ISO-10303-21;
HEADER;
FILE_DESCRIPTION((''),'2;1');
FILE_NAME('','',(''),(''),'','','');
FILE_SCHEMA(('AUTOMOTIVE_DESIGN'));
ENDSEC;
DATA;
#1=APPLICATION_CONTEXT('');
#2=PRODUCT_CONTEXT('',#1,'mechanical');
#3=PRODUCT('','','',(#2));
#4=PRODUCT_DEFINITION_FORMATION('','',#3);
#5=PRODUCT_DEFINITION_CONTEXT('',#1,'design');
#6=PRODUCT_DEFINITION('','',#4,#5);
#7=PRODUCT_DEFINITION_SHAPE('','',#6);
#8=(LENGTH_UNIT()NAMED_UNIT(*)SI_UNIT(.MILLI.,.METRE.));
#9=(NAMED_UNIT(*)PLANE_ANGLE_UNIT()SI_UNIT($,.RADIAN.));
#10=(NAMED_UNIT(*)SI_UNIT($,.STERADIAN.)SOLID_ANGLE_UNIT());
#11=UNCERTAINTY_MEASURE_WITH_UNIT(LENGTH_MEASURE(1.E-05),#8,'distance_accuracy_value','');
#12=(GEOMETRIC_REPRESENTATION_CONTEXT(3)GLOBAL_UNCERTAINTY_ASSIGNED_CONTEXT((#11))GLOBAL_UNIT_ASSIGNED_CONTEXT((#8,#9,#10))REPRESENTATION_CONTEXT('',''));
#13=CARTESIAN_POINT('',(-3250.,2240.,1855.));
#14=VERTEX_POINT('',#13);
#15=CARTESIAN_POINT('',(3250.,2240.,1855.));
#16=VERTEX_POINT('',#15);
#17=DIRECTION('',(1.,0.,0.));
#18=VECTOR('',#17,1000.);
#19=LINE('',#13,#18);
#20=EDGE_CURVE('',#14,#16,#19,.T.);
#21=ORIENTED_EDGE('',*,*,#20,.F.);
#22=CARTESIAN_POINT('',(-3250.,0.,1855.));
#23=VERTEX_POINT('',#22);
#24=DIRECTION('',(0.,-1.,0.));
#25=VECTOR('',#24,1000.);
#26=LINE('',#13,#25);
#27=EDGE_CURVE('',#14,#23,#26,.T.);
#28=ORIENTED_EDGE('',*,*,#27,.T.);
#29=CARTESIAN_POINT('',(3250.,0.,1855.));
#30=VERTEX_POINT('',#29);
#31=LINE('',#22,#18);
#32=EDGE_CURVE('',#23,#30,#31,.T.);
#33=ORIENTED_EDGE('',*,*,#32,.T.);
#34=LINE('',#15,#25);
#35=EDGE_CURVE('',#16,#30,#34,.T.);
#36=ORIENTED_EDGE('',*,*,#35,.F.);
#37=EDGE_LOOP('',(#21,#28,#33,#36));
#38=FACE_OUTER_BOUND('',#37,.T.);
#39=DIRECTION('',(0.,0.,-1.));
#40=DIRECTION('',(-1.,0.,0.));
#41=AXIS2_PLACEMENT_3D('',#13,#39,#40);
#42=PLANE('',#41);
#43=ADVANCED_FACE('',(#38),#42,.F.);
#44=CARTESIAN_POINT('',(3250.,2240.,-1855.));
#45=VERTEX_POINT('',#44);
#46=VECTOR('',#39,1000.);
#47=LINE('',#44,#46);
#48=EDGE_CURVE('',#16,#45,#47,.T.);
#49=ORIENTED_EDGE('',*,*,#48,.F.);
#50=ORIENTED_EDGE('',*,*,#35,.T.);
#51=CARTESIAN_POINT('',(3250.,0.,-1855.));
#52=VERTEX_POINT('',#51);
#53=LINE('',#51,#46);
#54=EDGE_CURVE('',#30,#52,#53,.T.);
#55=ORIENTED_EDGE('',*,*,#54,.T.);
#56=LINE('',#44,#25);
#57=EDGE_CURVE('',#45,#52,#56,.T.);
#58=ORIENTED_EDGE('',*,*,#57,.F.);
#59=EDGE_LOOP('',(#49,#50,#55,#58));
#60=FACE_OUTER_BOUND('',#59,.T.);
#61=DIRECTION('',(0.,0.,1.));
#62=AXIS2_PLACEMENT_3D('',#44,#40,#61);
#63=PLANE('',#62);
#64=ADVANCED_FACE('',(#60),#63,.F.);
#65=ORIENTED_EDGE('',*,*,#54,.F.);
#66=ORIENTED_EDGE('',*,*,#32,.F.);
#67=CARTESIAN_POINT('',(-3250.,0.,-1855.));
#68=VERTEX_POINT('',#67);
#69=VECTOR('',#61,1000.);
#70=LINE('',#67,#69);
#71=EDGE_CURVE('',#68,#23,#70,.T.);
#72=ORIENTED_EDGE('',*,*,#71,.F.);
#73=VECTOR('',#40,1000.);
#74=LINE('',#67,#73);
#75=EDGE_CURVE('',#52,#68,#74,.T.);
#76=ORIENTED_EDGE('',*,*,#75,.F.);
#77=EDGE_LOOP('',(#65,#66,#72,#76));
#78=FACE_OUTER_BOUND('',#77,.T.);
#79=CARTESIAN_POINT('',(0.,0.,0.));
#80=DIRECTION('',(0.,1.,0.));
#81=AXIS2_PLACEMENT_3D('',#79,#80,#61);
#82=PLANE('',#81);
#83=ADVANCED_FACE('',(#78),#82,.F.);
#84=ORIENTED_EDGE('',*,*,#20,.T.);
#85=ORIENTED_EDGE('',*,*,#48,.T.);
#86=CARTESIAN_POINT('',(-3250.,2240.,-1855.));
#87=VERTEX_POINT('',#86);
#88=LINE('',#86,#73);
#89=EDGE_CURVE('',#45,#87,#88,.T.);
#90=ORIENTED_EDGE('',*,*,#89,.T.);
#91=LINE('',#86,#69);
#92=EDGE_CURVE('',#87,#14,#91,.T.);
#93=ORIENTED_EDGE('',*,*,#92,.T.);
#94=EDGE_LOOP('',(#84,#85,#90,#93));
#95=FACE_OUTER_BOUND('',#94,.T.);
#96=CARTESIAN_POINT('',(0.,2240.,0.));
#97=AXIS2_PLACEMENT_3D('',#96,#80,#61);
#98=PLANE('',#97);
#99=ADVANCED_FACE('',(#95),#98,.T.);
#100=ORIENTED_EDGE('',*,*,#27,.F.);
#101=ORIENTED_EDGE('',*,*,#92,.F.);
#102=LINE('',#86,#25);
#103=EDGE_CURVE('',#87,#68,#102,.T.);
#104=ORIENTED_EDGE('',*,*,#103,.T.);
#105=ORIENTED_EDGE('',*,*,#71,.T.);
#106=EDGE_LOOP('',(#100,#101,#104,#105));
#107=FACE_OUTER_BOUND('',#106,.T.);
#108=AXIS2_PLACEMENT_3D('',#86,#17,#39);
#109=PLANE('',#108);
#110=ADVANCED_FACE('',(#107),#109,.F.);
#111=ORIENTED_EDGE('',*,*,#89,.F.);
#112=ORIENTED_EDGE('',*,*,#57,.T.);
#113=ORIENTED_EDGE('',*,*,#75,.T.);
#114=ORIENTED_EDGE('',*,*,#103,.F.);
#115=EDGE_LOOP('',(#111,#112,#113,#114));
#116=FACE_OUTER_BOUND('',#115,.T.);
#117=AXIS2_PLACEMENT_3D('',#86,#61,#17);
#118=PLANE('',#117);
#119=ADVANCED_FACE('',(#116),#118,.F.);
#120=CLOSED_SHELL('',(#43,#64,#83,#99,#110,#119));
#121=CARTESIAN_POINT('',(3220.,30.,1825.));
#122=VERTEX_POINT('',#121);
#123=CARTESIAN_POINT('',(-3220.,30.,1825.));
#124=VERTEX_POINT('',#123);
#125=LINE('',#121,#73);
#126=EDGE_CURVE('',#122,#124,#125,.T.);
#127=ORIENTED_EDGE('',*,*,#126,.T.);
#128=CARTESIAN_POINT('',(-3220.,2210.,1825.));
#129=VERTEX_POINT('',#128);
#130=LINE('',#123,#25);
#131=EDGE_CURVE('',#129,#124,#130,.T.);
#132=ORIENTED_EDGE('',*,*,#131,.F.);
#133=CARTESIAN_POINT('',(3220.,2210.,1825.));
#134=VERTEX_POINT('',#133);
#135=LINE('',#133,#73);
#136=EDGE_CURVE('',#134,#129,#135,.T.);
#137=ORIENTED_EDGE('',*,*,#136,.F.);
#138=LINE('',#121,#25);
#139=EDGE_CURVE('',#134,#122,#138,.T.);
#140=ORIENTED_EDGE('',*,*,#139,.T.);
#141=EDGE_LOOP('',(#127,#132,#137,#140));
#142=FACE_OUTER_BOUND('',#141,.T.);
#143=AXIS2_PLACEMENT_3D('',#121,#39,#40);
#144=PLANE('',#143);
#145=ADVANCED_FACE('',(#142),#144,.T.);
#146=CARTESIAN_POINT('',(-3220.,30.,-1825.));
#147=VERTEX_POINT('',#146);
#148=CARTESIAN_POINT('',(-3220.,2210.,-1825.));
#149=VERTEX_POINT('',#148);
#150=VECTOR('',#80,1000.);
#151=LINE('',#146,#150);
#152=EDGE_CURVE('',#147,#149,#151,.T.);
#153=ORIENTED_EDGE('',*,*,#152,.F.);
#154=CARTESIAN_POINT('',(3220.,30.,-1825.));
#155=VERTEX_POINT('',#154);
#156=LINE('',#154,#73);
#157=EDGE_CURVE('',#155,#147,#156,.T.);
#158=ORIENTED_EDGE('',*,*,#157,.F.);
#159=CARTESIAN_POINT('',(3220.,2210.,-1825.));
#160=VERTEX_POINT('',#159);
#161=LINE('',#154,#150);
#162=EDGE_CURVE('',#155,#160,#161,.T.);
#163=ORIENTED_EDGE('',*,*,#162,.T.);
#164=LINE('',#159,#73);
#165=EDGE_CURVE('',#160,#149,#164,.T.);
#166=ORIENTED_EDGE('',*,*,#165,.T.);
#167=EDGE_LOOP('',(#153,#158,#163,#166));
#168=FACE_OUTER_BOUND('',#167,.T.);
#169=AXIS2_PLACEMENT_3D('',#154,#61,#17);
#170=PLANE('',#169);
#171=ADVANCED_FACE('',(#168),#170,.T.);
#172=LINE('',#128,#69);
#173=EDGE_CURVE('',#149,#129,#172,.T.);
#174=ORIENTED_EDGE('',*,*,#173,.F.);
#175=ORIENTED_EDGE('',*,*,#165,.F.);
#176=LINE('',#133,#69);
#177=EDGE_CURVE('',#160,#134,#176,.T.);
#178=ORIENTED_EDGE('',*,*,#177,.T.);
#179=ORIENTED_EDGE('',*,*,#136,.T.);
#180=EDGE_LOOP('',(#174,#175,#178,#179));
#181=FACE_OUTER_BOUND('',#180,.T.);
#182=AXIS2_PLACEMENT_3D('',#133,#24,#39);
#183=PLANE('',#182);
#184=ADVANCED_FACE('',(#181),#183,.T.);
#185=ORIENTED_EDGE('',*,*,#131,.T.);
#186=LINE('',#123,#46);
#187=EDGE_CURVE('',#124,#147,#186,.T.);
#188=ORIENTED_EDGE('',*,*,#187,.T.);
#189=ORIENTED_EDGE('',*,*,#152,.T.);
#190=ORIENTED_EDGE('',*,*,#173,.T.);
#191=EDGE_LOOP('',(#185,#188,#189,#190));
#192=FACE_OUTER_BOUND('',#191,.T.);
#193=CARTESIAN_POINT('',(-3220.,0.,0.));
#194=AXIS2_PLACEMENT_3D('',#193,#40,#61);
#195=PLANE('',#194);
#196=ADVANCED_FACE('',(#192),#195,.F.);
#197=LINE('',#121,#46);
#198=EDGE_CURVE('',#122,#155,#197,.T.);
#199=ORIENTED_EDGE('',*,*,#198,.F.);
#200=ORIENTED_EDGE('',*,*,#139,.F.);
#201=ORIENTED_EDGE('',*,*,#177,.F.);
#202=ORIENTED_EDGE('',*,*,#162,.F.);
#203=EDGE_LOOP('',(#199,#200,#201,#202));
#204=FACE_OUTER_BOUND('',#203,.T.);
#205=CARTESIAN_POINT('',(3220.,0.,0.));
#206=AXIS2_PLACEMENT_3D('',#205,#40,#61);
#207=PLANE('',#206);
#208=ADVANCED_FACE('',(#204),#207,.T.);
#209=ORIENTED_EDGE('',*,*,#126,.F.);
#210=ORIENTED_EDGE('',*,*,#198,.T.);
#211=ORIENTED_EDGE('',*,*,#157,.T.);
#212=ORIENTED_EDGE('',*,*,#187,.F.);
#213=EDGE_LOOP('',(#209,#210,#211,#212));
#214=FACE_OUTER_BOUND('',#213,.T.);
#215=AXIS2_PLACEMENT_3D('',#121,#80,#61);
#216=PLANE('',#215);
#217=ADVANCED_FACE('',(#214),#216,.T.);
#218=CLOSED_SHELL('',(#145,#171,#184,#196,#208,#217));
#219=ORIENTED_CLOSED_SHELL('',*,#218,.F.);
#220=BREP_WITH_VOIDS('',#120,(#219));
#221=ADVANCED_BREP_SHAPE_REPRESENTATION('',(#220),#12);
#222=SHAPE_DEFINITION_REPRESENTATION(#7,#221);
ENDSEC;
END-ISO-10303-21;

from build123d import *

# Parameters (mm, degrees)
SKETCH_1_W               = 6500
SKETCH_1_H               = 3710
EXTRUDE_1_DEPTH          = 2240
CUT_EXTRUDE_1_DEPTH      = 3220
CUT_EXTRUDE_1_DEPTH_BACK = 3220
SKETCH_2_W               = 3650
SKETCH_2_H               = 2180


with BuildPart() as part:
    # 草图1 → 凸台-拉伸1 (new body)
    with BuildSketch(Plane(origin=(0, 0, 0), x_dir=(1, 0, 0), z_dir=(0, 1, 0))):
        Rectangle(SKETCH_1_W, SKETCH_1_H)
    extrude(amount=EXTRUDE_1_DEPTH)

    # 草图2 → 切除-拉伸1 (cut, two sides: drawn at the far end of the back side and taken through both)
    with BuildSketch(Plane(origin=(0, 0, 0), x_dir=(0, 0, -1), z_dir=(1, 0, 0)).offset(-CUT_EXTRUDE_1_DEPTH_BACK)):
        with Locations((0, 1120)):
            Rectangle(SKETCH_2_W, SKETCH_2_H)
    extrude(amount=CUT_EXTRUDE_1_DEPTH + CUT_EXTRUDE_1_DEPTH_BACK, mode=Mode.SUBTRACT)


solid = part.part
